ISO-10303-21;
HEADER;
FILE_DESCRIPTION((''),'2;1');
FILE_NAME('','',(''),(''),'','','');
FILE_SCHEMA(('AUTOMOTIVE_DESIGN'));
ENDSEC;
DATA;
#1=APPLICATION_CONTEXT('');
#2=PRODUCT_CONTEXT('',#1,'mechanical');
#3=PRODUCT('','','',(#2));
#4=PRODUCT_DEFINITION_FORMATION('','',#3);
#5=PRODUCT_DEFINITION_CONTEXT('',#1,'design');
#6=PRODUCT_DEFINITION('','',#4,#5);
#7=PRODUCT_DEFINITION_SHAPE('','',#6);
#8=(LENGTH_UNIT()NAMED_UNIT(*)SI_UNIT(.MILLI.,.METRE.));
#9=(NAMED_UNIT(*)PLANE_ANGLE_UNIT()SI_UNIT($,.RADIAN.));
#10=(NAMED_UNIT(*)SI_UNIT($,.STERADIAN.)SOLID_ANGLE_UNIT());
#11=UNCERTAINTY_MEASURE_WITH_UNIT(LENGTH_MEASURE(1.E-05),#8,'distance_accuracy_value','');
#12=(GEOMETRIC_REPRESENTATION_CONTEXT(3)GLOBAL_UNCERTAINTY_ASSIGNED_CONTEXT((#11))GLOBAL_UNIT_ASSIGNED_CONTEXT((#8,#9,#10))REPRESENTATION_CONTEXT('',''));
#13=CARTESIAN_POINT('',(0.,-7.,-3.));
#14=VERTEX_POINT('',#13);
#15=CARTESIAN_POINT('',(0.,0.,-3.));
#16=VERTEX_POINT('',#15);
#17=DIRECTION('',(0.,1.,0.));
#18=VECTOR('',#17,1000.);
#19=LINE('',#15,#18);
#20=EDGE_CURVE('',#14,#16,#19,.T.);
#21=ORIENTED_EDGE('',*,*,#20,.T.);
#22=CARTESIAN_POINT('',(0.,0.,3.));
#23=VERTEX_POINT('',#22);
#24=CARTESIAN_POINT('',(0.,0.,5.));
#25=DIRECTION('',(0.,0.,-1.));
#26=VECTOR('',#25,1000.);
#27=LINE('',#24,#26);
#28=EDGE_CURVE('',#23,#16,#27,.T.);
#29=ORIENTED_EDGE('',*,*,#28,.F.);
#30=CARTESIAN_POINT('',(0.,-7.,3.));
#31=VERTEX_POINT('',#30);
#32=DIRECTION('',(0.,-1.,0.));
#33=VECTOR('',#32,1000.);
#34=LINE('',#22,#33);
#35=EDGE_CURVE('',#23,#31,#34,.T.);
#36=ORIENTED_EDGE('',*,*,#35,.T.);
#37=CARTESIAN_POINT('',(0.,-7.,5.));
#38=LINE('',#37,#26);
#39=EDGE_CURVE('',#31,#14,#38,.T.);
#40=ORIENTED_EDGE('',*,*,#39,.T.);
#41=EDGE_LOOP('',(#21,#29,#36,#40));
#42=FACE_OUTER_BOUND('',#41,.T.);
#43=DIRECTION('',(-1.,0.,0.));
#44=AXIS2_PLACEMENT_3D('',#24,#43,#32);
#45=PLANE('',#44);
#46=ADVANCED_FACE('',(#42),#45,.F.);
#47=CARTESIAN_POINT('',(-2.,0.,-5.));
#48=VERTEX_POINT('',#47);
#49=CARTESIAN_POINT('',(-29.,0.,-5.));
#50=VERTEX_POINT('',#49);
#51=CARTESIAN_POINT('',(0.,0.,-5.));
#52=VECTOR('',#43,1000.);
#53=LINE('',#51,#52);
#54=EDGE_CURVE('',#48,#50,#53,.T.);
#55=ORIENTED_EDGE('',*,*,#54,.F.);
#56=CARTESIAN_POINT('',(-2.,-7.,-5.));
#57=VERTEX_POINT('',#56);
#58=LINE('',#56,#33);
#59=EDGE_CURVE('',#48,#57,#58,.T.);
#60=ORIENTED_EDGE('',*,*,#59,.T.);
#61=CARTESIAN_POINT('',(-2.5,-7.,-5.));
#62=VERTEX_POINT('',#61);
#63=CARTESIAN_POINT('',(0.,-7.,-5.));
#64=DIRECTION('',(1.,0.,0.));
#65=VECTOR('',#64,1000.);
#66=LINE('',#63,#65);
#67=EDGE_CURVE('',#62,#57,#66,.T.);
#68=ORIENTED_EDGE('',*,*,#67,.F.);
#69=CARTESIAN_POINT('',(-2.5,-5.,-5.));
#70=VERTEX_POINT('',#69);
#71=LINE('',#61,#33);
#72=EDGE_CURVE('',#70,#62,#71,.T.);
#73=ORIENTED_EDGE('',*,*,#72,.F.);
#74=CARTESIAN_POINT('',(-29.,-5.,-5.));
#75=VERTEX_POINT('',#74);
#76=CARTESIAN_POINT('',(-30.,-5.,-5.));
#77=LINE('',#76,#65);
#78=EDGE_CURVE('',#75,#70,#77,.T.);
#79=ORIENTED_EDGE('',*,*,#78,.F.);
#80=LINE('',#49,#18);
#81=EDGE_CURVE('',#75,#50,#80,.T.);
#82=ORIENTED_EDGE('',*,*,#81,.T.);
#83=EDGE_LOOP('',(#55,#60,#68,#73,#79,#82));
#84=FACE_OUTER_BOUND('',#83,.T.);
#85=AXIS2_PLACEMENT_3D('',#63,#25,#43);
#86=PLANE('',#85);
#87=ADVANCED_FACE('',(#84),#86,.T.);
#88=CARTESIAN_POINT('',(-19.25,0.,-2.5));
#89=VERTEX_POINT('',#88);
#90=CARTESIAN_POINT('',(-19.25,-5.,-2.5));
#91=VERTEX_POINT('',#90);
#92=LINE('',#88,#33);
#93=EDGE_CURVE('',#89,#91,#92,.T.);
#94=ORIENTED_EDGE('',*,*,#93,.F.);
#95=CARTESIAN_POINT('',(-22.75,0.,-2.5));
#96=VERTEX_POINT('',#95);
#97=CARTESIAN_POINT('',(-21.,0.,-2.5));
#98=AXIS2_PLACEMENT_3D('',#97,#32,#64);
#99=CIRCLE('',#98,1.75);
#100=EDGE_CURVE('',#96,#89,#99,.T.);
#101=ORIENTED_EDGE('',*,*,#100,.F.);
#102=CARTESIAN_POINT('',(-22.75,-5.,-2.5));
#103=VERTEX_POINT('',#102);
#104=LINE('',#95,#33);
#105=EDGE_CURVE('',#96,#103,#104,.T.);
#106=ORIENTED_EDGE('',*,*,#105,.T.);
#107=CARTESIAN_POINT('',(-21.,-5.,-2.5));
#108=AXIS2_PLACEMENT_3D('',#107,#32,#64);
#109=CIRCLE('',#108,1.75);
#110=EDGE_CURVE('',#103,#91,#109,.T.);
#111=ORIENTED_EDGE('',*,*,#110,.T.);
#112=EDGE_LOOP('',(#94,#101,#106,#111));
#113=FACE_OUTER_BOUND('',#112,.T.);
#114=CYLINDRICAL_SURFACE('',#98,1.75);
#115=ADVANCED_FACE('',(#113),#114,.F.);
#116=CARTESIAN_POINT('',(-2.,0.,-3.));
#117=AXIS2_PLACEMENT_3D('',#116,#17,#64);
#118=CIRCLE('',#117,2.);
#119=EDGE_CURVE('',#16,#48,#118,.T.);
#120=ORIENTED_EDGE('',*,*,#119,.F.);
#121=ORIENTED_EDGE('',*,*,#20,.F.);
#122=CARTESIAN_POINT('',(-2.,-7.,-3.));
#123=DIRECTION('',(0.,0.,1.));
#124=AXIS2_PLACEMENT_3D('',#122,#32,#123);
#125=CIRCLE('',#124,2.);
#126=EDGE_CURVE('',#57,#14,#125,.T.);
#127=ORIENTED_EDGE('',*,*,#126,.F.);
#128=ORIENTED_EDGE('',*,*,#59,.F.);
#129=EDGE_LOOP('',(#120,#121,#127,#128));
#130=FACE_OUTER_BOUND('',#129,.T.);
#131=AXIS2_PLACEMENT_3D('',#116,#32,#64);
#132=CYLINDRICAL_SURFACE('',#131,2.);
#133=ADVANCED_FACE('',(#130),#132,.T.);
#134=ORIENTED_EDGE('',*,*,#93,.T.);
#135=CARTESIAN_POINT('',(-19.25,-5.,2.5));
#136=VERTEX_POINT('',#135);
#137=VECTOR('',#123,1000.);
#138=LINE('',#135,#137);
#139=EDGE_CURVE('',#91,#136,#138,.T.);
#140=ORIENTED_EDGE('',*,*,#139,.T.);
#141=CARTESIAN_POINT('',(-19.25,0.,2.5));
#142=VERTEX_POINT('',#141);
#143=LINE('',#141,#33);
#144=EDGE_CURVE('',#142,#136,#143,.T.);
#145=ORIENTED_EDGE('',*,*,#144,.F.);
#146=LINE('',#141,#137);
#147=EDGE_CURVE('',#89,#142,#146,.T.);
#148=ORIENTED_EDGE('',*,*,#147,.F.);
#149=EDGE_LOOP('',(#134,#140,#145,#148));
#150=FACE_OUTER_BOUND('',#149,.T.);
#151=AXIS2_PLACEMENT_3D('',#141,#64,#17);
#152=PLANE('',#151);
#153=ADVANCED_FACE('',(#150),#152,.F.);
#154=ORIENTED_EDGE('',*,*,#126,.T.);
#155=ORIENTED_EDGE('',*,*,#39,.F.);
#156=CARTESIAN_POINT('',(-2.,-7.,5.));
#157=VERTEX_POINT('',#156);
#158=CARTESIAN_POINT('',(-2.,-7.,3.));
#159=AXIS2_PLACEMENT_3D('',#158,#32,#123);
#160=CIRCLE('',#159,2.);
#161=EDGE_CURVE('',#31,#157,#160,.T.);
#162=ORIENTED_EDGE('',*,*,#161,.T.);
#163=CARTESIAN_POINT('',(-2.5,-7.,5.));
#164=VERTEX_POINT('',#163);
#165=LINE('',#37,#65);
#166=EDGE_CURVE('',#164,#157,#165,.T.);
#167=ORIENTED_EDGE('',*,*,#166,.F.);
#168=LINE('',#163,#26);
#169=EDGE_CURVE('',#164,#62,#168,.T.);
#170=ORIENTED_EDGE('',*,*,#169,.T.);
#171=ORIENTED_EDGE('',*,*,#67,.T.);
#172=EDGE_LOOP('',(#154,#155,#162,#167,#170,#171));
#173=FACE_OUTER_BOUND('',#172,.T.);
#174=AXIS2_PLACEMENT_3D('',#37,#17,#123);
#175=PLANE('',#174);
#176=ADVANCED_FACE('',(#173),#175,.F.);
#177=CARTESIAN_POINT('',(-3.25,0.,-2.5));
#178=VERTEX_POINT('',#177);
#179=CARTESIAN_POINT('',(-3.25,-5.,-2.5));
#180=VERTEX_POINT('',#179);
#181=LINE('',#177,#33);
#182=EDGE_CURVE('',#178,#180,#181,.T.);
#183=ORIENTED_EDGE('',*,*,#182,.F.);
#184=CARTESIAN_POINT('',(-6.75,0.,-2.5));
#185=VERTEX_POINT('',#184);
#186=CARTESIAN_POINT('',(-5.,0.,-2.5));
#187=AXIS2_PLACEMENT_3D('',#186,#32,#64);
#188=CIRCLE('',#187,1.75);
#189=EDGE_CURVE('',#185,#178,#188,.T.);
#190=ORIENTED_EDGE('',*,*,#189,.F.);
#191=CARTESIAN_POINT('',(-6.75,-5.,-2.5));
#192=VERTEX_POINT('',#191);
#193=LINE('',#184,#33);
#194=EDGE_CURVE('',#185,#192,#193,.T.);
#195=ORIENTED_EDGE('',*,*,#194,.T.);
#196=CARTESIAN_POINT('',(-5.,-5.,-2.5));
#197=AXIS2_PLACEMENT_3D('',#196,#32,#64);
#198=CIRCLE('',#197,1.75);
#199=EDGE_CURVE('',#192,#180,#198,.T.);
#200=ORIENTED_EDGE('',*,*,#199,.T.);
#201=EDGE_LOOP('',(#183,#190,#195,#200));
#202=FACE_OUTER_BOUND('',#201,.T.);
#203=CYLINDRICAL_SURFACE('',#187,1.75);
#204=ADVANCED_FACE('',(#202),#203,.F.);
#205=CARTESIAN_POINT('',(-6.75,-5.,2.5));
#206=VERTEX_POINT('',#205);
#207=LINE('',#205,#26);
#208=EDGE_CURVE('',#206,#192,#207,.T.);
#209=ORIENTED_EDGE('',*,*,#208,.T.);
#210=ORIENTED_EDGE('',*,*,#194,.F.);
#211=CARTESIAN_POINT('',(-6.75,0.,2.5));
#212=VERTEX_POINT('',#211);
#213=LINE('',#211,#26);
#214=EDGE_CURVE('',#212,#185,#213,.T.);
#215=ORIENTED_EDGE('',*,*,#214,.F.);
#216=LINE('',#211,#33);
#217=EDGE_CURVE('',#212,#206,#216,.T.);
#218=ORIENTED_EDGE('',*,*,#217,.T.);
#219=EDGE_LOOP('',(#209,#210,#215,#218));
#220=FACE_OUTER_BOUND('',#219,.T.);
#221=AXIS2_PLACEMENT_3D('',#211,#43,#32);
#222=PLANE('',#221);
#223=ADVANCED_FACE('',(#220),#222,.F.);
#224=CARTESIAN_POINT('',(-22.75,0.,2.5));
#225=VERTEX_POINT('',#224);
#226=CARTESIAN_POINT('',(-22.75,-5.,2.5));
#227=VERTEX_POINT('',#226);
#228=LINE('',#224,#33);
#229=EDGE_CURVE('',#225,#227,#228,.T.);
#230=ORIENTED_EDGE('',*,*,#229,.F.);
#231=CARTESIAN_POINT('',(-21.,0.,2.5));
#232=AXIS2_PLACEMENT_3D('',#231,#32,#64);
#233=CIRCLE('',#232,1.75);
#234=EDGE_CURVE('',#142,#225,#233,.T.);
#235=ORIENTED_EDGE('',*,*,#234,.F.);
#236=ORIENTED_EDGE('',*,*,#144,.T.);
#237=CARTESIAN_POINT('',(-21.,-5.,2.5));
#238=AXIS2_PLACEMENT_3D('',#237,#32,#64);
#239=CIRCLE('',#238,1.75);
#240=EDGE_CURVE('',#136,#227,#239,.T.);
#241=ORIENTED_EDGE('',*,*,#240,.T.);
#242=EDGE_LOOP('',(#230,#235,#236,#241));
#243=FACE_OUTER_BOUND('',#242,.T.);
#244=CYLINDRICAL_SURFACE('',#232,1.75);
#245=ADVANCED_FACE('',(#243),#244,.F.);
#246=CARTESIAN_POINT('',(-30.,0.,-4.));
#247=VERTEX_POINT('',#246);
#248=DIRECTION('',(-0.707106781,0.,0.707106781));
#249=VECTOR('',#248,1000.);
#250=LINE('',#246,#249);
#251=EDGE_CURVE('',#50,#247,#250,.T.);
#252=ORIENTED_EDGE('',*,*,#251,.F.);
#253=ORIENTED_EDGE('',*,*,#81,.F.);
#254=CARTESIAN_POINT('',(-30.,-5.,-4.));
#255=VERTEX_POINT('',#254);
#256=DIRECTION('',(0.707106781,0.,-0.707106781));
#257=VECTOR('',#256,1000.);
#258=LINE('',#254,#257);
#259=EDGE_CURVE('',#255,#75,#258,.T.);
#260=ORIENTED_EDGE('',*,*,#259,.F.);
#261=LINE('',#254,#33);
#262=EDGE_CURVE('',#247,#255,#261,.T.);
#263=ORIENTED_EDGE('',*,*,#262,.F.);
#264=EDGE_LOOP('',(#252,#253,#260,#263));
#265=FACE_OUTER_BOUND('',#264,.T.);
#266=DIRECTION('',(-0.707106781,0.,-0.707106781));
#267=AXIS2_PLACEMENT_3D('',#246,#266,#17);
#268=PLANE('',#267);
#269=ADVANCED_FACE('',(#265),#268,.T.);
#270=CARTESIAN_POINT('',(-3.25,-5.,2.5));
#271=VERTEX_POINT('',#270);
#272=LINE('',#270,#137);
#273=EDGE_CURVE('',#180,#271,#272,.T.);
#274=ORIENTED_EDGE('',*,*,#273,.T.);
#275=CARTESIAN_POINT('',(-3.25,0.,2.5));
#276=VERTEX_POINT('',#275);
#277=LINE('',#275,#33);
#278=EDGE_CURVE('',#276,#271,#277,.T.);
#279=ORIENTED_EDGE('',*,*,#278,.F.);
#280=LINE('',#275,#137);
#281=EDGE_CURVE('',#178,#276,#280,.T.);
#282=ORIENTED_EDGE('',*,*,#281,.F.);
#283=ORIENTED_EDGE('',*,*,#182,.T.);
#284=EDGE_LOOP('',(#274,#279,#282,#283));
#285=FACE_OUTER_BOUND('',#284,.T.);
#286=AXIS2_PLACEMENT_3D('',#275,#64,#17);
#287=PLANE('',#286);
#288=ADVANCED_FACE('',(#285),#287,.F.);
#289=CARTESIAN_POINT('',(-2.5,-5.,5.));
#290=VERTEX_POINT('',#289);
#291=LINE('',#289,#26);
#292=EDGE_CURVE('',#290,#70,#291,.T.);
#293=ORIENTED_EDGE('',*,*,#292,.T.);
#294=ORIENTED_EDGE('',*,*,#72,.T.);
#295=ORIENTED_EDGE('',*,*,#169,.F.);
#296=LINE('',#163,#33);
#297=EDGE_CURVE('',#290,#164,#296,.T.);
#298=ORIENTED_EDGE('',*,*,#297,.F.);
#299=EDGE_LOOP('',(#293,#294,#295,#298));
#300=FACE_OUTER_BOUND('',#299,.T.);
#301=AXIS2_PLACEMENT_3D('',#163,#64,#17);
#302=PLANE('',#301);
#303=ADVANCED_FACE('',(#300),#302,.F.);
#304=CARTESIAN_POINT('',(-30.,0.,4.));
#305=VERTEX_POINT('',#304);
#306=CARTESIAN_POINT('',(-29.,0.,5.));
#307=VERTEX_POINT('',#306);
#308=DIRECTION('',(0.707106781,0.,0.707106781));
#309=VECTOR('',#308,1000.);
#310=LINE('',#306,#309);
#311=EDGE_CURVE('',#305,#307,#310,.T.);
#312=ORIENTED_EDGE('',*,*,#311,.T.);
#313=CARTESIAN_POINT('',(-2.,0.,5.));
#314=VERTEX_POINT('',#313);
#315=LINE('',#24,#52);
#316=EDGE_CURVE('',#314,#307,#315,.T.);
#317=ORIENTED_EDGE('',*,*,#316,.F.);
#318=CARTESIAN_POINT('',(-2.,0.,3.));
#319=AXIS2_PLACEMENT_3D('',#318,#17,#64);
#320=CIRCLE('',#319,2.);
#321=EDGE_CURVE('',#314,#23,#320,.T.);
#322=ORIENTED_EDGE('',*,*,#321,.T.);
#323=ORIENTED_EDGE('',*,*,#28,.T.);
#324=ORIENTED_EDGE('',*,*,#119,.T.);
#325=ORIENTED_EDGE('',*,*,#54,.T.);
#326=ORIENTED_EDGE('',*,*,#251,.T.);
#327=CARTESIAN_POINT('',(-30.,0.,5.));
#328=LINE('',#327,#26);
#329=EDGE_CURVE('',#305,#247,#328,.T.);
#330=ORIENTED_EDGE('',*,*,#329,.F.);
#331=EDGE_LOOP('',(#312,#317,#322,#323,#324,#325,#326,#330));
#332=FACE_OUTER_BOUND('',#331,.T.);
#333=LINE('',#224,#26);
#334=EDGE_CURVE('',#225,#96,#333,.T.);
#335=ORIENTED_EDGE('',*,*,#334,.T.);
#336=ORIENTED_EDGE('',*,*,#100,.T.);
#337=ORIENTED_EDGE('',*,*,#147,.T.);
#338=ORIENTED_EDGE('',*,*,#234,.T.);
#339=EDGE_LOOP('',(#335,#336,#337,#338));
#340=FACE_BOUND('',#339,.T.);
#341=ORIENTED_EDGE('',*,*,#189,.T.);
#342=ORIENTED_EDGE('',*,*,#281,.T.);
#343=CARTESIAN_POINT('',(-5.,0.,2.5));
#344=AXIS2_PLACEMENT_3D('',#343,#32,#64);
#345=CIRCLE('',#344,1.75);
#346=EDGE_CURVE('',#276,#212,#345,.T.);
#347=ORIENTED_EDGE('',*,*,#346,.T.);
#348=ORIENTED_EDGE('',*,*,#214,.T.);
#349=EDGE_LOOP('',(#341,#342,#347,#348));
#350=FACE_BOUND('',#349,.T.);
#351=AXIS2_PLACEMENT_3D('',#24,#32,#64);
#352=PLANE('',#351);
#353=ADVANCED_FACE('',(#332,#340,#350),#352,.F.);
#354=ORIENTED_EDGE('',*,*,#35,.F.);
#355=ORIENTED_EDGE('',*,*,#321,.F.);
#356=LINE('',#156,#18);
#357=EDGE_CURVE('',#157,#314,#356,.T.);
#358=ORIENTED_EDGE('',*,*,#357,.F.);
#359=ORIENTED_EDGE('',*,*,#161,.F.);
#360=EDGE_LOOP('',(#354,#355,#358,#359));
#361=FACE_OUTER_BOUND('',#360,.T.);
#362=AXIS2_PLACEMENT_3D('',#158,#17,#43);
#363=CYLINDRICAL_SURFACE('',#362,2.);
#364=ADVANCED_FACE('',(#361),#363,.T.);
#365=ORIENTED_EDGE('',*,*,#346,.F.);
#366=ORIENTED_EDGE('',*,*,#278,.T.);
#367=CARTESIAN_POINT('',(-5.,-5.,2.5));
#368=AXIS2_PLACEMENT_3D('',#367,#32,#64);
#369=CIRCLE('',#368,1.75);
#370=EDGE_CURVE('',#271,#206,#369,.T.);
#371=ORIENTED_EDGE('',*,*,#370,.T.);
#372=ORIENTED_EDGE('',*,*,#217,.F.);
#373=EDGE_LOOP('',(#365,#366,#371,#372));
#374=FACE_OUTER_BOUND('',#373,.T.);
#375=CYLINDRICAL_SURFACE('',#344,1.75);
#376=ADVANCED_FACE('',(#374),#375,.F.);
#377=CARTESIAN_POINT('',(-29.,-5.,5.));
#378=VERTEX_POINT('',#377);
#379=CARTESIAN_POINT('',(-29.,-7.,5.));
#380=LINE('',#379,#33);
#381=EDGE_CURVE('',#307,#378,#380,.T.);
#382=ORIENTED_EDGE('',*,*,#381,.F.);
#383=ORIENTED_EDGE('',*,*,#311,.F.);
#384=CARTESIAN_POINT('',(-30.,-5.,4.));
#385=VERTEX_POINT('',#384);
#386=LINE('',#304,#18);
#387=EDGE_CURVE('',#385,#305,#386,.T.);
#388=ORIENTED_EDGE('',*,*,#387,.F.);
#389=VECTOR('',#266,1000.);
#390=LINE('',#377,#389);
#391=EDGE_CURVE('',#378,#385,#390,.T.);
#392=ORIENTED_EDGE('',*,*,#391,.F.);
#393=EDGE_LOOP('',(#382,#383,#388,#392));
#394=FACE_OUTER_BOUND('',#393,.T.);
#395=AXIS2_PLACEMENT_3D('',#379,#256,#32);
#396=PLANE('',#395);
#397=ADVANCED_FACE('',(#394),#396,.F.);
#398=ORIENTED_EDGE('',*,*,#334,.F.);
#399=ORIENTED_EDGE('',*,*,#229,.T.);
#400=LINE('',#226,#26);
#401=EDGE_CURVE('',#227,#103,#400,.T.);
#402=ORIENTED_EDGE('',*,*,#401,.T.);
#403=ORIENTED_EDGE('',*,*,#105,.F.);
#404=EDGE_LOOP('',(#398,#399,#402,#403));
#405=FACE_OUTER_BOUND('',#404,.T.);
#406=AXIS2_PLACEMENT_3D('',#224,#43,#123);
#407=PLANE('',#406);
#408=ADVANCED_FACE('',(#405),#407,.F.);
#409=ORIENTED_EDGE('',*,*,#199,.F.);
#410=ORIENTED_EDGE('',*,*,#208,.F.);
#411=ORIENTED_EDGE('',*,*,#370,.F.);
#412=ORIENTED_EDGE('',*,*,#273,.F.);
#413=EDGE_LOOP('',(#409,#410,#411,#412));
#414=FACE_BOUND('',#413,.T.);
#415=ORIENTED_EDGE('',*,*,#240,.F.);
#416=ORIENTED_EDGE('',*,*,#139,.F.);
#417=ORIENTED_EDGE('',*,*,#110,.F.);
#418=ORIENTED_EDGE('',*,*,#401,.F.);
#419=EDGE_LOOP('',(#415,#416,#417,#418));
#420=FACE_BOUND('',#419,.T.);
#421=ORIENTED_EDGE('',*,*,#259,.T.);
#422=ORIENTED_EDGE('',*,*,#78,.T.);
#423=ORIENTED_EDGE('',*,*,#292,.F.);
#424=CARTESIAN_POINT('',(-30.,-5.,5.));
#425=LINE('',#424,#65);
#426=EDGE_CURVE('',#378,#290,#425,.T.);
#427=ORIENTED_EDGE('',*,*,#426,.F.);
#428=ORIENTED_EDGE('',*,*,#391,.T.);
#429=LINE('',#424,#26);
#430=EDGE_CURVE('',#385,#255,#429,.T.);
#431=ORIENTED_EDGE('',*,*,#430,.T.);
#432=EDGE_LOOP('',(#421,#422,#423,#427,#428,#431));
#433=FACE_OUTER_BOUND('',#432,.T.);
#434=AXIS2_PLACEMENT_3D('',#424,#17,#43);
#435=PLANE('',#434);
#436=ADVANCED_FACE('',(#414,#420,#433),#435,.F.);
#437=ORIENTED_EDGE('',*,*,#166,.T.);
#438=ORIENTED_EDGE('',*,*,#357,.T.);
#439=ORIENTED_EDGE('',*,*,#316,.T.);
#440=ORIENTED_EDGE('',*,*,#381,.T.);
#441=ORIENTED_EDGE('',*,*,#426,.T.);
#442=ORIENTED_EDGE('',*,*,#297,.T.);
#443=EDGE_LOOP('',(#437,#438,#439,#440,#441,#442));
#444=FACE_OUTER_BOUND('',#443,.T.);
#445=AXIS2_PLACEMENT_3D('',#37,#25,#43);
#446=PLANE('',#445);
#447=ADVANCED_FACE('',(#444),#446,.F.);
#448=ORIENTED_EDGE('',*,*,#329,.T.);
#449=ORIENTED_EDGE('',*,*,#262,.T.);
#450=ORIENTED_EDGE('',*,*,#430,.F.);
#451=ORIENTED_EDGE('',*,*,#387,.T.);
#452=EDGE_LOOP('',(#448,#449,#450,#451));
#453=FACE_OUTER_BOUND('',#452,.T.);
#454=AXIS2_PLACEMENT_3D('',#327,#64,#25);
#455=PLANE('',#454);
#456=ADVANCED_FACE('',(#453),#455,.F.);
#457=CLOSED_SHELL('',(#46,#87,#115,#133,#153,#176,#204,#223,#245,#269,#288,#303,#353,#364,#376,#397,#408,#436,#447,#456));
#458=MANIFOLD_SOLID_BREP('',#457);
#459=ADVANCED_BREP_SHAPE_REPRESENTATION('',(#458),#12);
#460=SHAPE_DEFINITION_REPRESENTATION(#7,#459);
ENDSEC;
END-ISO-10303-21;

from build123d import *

# Parameters (mm, degrees)
BOSS_EXTRUDE1_DEPTH = 5
CUT_EXTRUDE1_DEPTH  = 31.822070015
FILLET1_R           = 2
CHAMFER1_SIZE       = 1


with BuildPart() as part:
    # Sketch1 → Boss-Extrude1 (new, symmetric)
    with BuildSketch(Plane.XY):
        Polygon((0, 0), (-30, 0), (-30, -5), (-2.5, -5), (-2.5, -7), (0, -7), align=None)
    extrude(amount=BOSS_EXTRUDE1_DEPTH, both=True)

    # Sketch2 → Cut-Extrude1 (cut, through all)
    with BuildSketch(Plane.XZ.offset(5)):
        with BuildLine():
            Line((-19.25, 2.5), (-19.25, -2.5))
            ThreePointArc((-19.25, -2.5), (-21, -4.25), (-22.75, -2.5))
            Line((-22.75, -2.5), (-22.75, 2.5))
            ThreePointArc((-22.75, 2.5), (-21, 4.25), (-19.25, 2.5))
        make_face()
        with BuildLine():
            Line((-3.25, 2.5), (-3.25, -2.5))
            ThreePointArc((-3.25, -2.5), (-5, -4.25), (-6.75, -2.5))
            Line((-6.75, -2.5), (-6.75, 2.5))
            ThreePointArc((-6.75, 2.5), (-5, 4.25), (-3.25, 2.5))
        make_face()
    extrude(amount=-CUT_EXTRUDE1_DEPTH, mode=Mode.SUBTRACT)

    # Fillet1
    fillet1_edges = [part.edges().sort_by_distance(p)[0] for p in [
        (0, -3.5, 5),
        (0, -3.5, -5),
    ]]
    fillet(fillet1_edges, radius=FILLET1_R)

    # Chamfer1
    chamfer1_edges = [part.edges().sort_by_distance(p)[0] for p in [
        (-30, -2.5, 5),
        (-30, -2.5, -5),
    ]]
    chamfer(chamfer1_edges, length=CHAMFER1_SIZE)


solid = part.part
